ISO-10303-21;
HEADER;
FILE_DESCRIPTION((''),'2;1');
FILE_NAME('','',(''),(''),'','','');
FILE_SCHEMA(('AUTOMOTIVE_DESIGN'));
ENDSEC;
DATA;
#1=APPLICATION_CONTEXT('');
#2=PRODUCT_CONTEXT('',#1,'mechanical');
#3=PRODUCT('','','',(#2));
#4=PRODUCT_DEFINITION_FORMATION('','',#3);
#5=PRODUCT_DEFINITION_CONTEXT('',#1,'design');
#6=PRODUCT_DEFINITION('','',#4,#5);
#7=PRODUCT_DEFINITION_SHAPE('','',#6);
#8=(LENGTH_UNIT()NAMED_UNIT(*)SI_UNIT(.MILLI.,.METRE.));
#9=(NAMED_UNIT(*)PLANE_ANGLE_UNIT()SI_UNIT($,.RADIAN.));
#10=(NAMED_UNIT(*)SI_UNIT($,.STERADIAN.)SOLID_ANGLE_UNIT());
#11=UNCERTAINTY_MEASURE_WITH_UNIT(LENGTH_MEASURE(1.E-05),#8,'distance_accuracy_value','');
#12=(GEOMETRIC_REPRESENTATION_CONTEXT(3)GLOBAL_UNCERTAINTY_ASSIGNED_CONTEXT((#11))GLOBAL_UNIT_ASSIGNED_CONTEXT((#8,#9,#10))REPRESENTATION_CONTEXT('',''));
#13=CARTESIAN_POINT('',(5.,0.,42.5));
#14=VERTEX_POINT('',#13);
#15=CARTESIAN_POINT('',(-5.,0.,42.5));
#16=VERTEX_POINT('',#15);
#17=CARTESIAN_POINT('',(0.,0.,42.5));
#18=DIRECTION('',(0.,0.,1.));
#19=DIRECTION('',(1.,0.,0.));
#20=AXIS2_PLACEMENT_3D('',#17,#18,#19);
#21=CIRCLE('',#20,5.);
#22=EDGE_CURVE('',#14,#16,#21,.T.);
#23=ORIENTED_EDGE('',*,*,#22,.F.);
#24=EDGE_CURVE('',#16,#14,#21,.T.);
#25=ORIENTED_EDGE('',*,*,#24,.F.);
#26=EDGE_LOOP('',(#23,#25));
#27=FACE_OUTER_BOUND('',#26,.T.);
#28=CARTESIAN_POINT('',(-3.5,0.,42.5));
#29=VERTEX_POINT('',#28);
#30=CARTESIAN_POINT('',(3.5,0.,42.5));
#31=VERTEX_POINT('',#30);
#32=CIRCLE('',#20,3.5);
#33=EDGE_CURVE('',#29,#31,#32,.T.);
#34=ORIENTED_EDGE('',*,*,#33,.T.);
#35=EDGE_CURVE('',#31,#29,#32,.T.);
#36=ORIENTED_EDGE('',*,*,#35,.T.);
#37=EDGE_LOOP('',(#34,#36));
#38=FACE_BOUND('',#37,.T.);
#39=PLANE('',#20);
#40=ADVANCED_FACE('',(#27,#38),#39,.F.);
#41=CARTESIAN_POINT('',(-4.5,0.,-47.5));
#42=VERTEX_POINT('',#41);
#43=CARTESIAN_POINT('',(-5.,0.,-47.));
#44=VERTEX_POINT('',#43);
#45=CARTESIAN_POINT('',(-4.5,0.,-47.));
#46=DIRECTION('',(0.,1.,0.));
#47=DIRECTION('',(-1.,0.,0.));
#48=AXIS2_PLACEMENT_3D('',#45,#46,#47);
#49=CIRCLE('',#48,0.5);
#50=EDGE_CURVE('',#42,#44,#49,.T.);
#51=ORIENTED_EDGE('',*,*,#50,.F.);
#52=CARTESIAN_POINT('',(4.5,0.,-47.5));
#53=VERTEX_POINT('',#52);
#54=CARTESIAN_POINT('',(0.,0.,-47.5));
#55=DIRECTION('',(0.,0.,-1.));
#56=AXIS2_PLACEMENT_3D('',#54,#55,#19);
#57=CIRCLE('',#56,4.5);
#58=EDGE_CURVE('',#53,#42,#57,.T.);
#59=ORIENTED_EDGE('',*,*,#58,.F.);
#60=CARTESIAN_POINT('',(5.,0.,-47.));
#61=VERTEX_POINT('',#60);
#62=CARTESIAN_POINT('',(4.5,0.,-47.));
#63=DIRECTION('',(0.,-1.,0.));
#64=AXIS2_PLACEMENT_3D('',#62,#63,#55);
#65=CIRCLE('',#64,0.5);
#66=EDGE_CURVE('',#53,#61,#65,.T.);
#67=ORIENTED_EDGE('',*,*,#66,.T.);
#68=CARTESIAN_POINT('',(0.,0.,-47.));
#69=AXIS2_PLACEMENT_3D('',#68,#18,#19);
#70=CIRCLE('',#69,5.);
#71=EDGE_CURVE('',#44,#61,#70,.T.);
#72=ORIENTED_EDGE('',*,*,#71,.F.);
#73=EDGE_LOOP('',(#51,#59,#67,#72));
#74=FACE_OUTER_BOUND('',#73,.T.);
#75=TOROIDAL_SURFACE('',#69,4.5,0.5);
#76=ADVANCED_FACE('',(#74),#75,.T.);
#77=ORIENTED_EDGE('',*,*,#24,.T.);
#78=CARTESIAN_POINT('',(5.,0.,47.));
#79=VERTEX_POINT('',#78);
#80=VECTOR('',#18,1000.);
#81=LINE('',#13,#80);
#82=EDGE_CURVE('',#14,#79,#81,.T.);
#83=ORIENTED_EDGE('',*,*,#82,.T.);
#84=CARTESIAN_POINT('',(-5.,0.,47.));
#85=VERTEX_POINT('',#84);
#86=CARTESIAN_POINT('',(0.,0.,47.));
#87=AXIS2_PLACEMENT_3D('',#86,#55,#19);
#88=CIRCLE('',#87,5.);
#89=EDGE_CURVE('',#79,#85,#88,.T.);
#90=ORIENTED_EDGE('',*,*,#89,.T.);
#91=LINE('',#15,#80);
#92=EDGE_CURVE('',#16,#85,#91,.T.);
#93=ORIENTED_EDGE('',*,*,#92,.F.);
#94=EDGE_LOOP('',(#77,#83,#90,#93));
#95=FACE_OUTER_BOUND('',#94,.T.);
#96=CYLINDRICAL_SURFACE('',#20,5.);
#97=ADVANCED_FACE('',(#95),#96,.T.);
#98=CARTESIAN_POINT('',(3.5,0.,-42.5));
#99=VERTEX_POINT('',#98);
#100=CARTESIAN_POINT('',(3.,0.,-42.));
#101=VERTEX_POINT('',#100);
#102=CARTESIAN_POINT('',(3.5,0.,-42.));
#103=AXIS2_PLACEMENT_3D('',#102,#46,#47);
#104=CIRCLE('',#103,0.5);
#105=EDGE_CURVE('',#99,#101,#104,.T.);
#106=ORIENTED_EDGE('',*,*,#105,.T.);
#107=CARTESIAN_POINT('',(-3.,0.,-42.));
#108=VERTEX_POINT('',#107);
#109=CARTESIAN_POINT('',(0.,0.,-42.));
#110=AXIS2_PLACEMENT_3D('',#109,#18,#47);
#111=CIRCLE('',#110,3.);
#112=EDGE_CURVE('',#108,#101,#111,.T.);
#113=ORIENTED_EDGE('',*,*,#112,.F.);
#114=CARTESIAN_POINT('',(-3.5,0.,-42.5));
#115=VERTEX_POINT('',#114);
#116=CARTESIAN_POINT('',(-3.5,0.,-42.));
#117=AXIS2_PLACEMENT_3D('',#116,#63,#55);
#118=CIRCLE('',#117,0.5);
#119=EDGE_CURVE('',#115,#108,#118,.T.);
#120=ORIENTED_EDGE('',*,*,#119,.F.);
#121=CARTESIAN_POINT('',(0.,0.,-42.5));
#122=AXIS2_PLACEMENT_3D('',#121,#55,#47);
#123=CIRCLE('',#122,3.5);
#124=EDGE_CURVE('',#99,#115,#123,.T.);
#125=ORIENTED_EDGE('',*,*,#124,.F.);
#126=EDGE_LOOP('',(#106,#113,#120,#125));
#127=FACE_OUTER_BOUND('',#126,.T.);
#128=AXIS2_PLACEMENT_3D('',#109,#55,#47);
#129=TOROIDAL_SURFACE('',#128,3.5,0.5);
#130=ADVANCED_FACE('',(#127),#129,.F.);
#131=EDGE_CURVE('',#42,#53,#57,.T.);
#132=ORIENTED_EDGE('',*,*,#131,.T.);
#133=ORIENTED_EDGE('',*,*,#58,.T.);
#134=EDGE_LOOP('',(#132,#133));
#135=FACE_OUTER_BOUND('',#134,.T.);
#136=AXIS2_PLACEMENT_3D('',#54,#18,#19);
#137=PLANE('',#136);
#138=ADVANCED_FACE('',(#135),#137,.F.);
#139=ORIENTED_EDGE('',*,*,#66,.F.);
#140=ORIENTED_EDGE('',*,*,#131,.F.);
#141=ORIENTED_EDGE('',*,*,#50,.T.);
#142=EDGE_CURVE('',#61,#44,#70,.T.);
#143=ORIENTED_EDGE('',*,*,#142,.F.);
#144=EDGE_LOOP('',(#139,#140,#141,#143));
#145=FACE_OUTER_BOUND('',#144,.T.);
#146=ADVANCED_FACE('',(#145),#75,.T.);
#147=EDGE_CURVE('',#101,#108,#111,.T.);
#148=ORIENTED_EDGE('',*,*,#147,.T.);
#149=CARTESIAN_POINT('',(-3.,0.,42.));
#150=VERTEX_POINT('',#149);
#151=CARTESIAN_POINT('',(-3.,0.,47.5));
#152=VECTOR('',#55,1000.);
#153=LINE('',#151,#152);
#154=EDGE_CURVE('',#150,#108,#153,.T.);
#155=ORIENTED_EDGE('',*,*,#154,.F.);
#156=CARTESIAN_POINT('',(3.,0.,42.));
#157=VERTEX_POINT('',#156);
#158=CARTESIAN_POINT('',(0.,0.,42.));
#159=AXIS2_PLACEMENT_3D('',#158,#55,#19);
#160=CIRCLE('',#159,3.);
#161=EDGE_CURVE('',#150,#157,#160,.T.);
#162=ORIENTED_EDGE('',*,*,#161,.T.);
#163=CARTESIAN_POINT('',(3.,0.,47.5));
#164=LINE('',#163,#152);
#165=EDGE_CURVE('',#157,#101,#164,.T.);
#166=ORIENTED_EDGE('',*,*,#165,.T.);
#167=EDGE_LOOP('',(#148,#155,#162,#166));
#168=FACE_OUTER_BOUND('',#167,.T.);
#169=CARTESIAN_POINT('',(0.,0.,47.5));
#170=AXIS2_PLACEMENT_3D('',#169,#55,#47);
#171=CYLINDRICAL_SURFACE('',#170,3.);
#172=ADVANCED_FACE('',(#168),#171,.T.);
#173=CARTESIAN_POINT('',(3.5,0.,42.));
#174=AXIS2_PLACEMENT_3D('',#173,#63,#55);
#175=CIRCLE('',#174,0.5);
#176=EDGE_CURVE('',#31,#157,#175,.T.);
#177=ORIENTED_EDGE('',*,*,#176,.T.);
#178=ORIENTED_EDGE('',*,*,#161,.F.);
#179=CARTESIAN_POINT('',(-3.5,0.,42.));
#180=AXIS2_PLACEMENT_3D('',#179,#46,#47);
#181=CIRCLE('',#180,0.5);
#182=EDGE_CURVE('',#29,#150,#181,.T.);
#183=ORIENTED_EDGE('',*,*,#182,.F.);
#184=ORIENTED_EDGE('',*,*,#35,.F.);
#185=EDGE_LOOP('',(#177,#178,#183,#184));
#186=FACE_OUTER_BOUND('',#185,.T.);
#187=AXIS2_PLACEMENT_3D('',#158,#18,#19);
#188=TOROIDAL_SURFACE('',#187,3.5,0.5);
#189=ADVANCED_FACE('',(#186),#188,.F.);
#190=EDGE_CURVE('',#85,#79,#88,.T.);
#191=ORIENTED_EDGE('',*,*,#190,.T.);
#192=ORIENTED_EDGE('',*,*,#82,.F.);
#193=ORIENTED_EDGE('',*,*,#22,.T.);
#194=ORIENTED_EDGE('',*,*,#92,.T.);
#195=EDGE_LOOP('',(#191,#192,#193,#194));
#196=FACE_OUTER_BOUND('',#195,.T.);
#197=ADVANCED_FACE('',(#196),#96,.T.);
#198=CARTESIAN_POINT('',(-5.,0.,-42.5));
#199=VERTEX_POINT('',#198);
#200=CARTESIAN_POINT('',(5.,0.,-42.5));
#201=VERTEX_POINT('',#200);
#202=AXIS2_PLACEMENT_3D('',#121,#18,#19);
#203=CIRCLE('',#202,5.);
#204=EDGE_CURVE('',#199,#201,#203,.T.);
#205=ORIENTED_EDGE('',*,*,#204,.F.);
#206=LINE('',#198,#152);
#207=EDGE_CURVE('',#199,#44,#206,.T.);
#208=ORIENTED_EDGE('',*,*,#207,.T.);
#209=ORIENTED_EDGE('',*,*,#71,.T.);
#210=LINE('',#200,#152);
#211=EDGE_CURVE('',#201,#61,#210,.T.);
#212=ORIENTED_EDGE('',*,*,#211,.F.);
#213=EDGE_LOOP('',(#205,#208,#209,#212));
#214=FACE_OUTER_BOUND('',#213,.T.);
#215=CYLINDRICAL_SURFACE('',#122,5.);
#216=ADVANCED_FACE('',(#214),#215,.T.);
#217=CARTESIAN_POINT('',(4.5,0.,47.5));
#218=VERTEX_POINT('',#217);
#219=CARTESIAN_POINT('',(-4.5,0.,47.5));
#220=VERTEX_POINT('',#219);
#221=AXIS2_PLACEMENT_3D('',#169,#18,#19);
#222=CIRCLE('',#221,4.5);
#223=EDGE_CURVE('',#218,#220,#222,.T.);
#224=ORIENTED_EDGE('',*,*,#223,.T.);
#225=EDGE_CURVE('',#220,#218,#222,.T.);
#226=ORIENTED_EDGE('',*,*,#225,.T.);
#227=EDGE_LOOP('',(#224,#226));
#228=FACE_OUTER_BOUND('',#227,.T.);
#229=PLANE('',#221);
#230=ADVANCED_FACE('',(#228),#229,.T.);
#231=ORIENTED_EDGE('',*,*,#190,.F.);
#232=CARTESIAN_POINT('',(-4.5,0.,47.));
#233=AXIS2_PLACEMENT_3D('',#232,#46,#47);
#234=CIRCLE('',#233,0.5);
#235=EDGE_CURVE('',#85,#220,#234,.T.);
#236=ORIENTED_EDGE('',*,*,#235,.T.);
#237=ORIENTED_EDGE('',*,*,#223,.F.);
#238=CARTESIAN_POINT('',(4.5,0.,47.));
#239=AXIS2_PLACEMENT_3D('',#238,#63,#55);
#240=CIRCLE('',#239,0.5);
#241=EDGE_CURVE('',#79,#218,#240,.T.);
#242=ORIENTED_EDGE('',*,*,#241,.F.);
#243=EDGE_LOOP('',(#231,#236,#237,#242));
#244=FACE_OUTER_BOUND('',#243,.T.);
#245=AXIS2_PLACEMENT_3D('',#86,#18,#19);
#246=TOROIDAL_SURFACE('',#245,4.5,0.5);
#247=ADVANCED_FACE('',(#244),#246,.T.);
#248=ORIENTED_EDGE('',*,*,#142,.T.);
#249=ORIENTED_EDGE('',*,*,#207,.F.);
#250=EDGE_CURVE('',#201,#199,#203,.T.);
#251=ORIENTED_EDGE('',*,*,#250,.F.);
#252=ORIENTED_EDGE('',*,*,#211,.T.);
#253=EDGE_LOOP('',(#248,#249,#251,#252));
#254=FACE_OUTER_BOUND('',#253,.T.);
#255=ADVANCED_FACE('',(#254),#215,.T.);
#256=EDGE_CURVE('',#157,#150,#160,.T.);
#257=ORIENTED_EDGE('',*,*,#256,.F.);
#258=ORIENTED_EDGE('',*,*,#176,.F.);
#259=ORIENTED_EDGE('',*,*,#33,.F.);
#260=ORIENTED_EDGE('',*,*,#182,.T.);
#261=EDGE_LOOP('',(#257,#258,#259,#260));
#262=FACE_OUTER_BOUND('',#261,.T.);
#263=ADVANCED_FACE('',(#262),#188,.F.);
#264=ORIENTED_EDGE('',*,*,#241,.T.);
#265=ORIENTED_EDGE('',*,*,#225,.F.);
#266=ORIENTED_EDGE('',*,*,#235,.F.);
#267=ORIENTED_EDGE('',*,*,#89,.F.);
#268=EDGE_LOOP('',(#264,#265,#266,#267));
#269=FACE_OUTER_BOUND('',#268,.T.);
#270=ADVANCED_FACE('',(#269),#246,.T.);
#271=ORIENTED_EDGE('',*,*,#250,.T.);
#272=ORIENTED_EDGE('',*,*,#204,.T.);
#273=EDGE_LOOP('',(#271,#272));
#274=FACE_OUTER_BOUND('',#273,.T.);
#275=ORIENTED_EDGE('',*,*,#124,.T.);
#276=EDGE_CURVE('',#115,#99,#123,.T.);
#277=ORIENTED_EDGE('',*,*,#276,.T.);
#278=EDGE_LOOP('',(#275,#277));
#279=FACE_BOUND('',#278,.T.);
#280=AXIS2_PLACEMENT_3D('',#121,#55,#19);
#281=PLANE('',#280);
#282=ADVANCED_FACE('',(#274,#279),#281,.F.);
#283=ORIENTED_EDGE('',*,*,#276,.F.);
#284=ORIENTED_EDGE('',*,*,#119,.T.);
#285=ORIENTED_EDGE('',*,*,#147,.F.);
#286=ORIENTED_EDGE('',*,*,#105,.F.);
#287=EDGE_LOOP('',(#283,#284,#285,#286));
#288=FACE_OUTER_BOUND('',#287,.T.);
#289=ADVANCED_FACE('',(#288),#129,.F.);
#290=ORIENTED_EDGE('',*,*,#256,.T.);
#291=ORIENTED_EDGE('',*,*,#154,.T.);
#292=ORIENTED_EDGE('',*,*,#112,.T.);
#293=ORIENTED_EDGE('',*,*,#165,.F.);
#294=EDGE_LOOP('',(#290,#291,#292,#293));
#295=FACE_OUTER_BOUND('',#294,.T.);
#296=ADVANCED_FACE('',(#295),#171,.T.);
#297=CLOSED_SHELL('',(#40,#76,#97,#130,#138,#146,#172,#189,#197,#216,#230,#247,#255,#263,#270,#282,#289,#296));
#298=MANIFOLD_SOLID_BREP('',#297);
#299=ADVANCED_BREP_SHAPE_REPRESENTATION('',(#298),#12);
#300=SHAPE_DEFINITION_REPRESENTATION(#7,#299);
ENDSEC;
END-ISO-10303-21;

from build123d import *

# Parameters (mm, degrees)
SHAFT_PROFILE_6_R        = 3
SHAFT_6X95_DEPTH         = 47.5
HEAD_PROFILE_10_R        = 5
HEAD_10X5_DEPTH          = 5
HEAD_EDGE_FILLETS_R0_5_R = 0.5


with BuildPart() as part:
    # Shaft Profile Ø6 → Shaft Ø6x95 (new, symmetric)
    with BuildSketch(Plane.XY):
        Circle(SHAFT_PROFILE_6_R)
    extrude(amount=SHAFT_6X95_DEPTH, both=True)

    # Head Profile Ø10 → Head Ø10x5 (add)
    with BuildSketch(Plane.XY.offset(47.5)):
        Circle(HEAD_PROFILE_10_R)
    head_10x5 = extrude(amount=-HEAD_10X5_DEPTH)

    # Head Mirror: Head Ø10x5 across plane
    add(head_10x5.mirror(Plane.XY))

    # Head Edge Fillets R0.5
    head_edge_fillets_r0_5_edges = [part.edges().sort_by_distance(p)[0] for p in [
        (-3, 0, -42.5),
        (-5, 0, -47.5),
        (-3, 0, 42.5),
        (-5, 0, 47.5),
    ]]
    fillet(head_edge_fillets_r0_5_edges, radius=HEAD_EDGE_FILLETS_R0_5_R)


solid = part.part
